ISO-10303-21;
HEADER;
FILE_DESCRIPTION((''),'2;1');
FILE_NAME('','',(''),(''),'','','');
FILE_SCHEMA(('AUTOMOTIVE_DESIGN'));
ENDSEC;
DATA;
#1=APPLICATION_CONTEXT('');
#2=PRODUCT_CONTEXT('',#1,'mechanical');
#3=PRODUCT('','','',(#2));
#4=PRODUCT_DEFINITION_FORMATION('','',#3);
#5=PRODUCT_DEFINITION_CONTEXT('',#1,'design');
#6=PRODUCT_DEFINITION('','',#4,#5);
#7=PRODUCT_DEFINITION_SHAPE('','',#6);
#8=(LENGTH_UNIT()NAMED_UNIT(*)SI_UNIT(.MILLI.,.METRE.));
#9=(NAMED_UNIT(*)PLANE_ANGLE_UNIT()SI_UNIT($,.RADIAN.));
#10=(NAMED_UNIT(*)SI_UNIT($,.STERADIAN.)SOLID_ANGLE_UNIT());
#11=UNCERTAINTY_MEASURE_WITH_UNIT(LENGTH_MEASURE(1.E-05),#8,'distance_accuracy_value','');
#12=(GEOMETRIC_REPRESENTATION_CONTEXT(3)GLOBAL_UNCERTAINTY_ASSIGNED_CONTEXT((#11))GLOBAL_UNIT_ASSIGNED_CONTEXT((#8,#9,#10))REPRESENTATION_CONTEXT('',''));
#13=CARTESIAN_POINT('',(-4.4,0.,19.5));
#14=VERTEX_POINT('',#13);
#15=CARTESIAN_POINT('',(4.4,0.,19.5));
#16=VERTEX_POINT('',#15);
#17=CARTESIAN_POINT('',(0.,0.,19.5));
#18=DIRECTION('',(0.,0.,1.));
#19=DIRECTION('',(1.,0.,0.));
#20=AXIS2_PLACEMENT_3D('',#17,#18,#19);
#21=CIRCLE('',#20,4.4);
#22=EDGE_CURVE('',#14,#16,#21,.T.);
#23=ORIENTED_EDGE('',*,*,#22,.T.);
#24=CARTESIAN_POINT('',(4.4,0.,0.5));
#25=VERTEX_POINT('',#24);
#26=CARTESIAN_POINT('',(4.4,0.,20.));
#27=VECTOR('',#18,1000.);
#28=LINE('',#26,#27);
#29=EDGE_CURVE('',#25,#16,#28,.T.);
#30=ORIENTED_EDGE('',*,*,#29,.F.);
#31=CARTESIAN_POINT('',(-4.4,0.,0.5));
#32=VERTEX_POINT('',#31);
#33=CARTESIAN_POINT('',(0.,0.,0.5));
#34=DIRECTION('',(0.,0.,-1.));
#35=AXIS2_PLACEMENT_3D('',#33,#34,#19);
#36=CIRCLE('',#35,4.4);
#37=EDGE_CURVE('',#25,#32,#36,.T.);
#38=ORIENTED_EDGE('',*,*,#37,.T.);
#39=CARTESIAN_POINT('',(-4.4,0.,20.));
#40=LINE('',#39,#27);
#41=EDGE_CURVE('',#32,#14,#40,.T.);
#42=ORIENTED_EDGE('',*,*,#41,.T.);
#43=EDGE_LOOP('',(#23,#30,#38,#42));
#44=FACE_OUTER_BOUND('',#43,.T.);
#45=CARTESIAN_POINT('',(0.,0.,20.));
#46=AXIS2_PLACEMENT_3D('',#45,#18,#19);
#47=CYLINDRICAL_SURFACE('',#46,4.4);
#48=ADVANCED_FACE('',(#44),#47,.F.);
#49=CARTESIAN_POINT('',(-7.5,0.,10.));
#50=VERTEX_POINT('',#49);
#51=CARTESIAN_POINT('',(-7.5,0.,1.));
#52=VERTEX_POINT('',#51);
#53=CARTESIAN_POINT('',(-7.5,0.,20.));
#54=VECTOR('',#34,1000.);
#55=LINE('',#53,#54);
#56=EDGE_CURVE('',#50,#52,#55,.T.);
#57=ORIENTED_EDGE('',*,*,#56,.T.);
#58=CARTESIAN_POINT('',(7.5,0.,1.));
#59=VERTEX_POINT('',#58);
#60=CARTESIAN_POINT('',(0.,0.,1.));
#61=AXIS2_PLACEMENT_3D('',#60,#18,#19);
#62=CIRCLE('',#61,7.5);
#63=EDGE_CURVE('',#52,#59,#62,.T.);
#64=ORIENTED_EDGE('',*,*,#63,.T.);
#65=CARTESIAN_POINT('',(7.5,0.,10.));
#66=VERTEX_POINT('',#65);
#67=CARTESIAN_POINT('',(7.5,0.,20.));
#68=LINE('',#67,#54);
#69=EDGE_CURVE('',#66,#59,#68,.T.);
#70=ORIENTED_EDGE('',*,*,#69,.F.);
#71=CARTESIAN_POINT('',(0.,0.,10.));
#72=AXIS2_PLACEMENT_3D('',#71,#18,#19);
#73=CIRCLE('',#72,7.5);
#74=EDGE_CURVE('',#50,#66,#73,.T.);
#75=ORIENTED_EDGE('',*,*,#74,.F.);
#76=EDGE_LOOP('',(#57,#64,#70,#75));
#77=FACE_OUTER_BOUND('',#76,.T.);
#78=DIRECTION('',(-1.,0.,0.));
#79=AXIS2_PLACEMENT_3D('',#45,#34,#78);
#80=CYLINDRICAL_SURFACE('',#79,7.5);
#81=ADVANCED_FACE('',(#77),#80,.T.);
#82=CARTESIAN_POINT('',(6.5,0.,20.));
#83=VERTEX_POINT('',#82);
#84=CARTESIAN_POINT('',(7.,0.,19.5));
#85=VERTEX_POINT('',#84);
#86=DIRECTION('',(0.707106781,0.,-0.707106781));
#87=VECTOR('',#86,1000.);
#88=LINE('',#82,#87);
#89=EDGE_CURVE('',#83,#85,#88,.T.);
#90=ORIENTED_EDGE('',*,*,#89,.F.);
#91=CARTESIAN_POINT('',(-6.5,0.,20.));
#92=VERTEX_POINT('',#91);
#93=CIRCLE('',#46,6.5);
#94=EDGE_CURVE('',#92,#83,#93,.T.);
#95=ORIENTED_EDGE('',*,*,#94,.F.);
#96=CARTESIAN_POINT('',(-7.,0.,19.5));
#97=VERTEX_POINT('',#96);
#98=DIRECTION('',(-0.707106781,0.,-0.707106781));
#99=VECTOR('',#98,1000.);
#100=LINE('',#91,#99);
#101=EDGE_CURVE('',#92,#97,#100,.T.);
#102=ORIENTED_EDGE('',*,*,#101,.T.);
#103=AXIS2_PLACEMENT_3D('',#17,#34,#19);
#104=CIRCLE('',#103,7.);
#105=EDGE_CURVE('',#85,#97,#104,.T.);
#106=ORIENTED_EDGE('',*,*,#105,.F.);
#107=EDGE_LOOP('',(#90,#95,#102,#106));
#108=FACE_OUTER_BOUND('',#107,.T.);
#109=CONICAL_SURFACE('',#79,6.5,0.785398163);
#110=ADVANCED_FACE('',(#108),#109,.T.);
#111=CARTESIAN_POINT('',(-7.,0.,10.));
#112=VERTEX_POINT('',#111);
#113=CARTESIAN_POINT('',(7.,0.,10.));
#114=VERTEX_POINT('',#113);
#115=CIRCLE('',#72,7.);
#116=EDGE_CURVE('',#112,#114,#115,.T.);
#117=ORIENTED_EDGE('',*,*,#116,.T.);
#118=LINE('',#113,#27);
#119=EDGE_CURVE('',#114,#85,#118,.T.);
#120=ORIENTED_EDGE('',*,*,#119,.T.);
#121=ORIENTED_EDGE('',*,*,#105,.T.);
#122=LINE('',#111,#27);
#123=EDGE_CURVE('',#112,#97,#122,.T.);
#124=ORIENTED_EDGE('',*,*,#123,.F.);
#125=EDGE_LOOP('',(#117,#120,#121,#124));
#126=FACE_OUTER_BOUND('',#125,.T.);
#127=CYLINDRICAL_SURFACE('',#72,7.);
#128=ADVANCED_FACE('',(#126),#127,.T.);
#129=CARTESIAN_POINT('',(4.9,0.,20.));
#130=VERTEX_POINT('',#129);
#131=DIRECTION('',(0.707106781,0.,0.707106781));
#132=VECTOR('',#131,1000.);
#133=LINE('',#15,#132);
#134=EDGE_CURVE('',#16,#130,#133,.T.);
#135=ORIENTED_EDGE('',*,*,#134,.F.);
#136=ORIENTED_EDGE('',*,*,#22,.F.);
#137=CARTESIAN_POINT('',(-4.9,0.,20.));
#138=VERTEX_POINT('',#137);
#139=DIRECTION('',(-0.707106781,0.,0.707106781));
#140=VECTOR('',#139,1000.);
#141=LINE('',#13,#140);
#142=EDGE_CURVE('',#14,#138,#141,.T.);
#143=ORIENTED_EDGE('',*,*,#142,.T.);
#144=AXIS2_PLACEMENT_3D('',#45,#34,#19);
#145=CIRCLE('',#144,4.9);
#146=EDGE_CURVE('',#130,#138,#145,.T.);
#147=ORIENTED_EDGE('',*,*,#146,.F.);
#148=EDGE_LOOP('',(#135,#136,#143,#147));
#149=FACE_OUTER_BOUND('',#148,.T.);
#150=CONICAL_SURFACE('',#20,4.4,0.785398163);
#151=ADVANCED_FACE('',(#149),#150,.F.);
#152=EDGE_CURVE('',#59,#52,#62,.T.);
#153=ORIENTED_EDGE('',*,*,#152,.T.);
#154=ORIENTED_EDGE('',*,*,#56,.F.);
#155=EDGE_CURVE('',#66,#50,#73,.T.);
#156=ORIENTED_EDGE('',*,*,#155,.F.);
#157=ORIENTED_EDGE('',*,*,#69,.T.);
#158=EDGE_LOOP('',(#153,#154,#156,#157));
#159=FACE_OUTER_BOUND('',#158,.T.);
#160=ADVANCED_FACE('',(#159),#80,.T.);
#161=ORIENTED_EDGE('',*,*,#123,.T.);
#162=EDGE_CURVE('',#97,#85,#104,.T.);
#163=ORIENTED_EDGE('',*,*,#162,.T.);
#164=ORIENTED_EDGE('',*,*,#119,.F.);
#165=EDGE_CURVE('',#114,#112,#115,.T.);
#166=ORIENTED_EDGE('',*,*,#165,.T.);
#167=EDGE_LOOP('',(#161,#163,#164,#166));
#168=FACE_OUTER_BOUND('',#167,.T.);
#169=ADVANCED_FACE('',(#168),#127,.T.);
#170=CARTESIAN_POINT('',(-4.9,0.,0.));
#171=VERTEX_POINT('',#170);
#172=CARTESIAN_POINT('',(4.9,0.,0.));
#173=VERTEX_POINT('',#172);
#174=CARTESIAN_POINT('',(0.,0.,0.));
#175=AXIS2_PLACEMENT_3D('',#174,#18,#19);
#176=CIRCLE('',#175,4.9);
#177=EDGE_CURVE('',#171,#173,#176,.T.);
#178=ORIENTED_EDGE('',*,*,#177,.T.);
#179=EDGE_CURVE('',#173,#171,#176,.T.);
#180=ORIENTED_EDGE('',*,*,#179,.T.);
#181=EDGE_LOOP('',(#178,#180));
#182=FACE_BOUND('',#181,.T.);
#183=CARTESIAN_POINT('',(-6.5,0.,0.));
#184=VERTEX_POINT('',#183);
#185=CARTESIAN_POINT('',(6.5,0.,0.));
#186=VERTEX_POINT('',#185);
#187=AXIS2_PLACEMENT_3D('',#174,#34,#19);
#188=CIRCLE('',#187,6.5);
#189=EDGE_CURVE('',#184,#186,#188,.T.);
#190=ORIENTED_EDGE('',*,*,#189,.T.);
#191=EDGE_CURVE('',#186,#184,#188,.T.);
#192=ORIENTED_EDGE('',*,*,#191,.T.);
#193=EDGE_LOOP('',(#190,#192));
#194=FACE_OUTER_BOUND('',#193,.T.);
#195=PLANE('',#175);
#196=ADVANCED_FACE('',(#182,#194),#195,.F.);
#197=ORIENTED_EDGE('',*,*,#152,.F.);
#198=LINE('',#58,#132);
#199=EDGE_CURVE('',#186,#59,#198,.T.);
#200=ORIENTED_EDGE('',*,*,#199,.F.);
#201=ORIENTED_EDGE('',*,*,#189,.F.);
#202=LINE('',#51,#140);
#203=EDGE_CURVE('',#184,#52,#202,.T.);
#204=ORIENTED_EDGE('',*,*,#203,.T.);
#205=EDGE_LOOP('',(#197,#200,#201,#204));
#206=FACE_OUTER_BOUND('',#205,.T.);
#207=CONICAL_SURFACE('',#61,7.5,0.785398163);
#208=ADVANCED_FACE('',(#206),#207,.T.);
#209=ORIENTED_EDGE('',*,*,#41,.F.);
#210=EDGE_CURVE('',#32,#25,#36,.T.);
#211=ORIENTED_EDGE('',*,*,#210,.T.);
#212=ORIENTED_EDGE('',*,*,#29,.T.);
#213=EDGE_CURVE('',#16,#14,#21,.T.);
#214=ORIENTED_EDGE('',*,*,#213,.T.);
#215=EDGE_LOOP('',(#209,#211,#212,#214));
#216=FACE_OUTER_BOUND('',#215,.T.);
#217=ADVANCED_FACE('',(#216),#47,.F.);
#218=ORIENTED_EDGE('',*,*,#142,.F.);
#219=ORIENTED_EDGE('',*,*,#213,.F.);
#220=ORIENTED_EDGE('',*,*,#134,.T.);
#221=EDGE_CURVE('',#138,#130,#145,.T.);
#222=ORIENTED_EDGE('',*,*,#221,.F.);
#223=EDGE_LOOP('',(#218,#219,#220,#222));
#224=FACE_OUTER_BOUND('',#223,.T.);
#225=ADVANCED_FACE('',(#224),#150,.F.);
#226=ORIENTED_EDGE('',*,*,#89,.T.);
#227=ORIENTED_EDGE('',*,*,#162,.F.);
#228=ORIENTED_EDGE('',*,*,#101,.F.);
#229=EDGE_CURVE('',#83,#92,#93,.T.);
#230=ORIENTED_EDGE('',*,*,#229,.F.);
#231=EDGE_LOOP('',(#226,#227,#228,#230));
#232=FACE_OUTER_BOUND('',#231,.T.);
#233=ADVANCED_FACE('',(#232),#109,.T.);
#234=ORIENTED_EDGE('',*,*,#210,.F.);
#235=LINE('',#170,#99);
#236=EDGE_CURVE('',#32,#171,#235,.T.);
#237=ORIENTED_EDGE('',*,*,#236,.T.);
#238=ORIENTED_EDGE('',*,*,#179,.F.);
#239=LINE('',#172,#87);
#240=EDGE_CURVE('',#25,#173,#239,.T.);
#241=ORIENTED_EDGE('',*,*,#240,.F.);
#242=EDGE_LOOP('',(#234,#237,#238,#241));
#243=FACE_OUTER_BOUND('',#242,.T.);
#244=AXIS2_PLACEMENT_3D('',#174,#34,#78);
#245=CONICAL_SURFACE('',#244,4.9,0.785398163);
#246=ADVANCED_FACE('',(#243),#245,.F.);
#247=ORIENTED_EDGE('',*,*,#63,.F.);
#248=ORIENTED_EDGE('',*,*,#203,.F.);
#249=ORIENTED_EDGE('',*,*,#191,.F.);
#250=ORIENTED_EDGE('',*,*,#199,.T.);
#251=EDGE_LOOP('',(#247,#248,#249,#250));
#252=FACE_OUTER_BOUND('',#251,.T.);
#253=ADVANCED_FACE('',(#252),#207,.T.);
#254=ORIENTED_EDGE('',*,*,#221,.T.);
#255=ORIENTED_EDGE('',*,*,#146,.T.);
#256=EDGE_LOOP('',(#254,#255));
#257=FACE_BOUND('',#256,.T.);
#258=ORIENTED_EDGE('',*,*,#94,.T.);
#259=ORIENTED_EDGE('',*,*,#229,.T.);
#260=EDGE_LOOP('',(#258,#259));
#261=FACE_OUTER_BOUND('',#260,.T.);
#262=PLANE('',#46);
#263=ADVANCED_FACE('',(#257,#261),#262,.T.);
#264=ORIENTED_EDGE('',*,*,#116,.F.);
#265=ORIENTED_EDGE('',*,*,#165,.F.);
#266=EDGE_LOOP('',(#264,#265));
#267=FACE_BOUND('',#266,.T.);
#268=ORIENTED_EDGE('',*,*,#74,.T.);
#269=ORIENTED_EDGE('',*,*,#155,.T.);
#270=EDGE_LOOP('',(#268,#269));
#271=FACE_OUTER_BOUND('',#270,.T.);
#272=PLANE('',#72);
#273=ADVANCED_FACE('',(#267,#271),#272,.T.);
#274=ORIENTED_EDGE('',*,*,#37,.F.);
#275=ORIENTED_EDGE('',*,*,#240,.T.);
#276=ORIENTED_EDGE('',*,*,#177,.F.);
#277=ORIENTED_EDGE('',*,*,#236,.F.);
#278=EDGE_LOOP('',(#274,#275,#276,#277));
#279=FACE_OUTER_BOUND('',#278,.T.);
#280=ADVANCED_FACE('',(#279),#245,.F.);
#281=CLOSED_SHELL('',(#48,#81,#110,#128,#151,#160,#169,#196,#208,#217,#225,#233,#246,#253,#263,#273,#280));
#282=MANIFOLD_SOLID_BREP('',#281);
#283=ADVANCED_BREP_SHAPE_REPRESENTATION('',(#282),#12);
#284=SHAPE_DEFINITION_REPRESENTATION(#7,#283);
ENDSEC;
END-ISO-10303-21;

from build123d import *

# Parameters (mm, degrees)
SKETCH_1_R           = 7.5
EXTRUDE_1_DEPTH      = 20
SKETCH_2_OUTSIDE_W   = 22.83
SKETCH_2_OUTSIDE_H   = 22.83
SKETCH_2_OUTSIDE_R   = 7
CUT_EXTRUDE_1_DEPTH  = 10
HOLE_WIZARD_G1_8_1_D = 8.8
CHAMFER_1_SIZE       = 1
CHAMFER_2_SIZE       = 0.5


with BuildPart() as part:
    # 草图1 → 凸台-拉伸1 (new body)
    with BuildSketch(Plane.XY):
        Circle(SKETCH_1_R)
    extrude(amount=EXTRUDE_1_DEPTH)

    # 草图2 outside → 切除-拉伸1 (cut)
    with BuildSketch(Plane.XY.offset(20)):
        Rectangle(SKETCH_2_OUTSIDE_W, SKETCH_2_OUTSIDE_H)
        Circle(SKETCH_2_OUTSIDE_R, mode=Mode.SUBTRACT)
    extrude(amount=-CUT_EXTRUDE_1_DEPTH, mode=Mode.SUBTRACT)

    # G1/8 螺纹孔1 (through all)
    with Locations(Plane.XY.offset(20)):
        with Locations((0, 0)):
            Hole(HOLE_WIZARD_G1_8_1_D / 2)

    # 倒角1
    chamfer_1_edges = [part.edges().sort_by_distance(p)[0] for p in [
        (-7.5, 0, 0),
    ]]
    chamfer(chamfer_1_edges, length=CHAMFER_1_SIZE)

    # 倒角2
    chamfer_2_edges = [part.edges().sort_by_distance(p)[0] for p in [
        (-7, 0, 20),
        (4.4, 0, 20),
        (4.4, 0, 0),
    ]]
    chamfer(chamfer_2_edges, length=CHAMFER_2_SIZE)


solid = part.part
